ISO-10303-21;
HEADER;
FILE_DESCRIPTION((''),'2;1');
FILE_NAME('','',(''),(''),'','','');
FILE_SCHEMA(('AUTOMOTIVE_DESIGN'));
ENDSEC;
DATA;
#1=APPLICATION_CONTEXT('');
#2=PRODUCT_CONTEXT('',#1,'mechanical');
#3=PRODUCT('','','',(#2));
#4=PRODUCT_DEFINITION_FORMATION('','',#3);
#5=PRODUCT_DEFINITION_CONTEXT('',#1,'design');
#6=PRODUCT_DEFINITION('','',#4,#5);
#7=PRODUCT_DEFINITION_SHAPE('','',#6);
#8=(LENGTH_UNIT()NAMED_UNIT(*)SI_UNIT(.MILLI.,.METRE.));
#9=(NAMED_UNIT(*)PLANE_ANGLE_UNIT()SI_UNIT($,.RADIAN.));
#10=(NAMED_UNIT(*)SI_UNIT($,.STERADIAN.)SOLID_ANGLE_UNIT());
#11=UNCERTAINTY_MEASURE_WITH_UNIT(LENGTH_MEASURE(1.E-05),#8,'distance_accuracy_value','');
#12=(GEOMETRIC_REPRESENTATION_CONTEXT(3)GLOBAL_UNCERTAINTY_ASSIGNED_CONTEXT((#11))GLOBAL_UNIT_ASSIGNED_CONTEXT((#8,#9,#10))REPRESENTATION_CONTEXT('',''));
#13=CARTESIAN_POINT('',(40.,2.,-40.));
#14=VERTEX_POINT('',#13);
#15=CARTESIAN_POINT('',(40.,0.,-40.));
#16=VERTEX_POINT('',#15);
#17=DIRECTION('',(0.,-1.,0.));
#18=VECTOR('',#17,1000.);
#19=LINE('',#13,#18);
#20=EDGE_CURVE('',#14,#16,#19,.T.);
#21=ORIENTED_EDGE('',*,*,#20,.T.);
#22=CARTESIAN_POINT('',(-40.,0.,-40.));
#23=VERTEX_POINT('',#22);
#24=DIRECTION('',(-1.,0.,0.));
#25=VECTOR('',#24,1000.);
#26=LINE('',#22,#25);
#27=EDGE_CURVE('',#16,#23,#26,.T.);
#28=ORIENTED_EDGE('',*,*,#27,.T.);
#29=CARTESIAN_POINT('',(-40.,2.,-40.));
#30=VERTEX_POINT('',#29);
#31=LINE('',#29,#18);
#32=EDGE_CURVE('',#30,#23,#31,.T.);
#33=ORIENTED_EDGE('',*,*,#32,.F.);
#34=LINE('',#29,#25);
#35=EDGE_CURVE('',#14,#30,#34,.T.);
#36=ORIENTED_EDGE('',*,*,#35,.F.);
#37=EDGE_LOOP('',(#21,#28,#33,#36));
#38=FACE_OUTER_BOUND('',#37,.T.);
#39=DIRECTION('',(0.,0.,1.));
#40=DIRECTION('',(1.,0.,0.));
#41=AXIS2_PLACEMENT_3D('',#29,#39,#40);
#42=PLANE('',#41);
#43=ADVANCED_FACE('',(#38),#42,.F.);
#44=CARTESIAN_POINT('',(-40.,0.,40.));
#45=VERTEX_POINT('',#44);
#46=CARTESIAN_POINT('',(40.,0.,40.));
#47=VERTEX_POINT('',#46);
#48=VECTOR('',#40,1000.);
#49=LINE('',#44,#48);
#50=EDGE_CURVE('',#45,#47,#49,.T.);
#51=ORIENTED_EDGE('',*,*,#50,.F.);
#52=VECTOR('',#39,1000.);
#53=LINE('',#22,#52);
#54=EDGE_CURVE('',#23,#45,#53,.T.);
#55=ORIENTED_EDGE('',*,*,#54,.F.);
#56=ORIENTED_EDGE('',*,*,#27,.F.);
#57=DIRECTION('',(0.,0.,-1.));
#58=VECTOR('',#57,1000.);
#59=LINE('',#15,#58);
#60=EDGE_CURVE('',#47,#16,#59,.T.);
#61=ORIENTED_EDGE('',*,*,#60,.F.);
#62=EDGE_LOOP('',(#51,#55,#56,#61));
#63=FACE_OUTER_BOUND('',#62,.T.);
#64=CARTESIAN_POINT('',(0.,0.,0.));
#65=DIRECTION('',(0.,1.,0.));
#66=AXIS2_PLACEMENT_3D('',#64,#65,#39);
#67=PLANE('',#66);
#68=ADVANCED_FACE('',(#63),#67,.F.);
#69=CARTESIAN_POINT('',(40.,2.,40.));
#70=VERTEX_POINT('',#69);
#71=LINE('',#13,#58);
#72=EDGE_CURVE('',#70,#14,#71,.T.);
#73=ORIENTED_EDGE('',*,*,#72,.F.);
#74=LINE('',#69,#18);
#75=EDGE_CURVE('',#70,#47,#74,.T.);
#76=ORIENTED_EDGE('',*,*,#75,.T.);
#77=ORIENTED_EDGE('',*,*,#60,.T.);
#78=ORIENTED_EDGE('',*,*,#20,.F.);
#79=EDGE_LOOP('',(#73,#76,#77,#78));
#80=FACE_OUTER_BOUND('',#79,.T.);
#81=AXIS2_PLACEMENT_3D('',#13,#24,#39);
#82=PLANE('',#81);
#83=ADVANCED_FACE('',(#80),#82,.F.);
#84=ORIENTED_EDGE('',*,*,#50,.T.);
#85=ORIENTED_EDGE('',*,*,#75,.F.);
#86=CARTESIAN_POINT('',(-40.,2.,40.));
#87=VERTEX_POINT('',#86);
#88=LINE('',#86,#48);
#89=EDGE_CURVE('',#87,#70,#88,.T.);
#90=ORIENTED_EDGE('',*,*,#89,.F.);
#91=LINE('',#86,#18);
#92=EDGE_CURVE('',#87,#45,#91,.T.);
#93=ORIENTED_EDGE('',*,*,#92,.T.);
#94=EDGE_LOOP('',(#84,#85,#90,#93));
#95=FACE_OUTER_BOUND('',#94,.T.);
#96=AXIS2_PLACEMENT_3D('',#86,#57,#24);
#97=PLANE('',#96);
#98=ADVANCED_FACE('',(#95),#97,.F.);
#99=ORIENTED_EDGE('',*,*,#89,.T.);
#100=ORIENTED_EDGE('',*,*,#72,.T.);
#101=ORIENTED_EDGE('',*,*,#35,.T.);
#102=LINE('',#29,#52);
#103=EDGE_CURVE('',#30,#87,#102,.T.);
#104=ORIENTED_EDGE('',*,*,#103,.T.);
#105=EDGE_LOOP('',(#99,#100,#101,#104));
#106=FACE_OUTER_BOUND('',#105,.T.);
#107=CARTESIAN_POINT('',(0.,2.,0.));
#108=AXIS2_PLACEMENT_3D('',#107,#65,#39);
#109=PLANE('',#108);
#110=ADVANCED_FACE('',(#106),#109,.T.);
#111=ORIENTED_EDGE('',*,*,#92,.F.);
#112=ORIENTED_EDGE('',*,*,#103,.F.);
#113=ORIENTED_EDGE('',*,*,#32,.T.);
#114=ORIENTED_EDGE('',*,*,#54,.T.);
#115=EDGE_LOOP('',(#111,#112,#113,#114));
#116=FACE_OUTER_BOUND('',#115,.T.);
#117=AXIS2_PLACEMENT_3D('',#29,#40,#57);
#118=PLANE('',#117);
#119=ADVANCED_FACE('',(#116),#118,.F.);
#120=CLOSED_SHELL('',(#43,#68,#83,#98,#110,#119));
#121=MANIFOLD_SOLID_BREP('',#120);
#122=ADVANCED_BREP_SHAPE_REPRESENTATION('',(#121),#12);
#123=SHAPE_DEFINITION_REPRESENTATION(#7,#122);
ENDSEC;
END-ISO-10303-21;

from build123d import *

# Parameters (mm, degrees)
SKETCH1_W           = 80
SKETCH1_H           = 80
BOSS_EXTRUDE1_DEPTH = 2


with BuildPart() as part:
    # Sketch1 → Boss-Extrude1 (new body)
    with BuildSketch(Plane(origin=(0, 0, 0), x_dir=(1, 0, 0), z_dir=(0, 1, 0))):
        Rectangle(SKETCH1_W, SKETCH1_H)
    extrude(amount=BOSS_EXTRUDE1_DEPTH)


solid = part.part
